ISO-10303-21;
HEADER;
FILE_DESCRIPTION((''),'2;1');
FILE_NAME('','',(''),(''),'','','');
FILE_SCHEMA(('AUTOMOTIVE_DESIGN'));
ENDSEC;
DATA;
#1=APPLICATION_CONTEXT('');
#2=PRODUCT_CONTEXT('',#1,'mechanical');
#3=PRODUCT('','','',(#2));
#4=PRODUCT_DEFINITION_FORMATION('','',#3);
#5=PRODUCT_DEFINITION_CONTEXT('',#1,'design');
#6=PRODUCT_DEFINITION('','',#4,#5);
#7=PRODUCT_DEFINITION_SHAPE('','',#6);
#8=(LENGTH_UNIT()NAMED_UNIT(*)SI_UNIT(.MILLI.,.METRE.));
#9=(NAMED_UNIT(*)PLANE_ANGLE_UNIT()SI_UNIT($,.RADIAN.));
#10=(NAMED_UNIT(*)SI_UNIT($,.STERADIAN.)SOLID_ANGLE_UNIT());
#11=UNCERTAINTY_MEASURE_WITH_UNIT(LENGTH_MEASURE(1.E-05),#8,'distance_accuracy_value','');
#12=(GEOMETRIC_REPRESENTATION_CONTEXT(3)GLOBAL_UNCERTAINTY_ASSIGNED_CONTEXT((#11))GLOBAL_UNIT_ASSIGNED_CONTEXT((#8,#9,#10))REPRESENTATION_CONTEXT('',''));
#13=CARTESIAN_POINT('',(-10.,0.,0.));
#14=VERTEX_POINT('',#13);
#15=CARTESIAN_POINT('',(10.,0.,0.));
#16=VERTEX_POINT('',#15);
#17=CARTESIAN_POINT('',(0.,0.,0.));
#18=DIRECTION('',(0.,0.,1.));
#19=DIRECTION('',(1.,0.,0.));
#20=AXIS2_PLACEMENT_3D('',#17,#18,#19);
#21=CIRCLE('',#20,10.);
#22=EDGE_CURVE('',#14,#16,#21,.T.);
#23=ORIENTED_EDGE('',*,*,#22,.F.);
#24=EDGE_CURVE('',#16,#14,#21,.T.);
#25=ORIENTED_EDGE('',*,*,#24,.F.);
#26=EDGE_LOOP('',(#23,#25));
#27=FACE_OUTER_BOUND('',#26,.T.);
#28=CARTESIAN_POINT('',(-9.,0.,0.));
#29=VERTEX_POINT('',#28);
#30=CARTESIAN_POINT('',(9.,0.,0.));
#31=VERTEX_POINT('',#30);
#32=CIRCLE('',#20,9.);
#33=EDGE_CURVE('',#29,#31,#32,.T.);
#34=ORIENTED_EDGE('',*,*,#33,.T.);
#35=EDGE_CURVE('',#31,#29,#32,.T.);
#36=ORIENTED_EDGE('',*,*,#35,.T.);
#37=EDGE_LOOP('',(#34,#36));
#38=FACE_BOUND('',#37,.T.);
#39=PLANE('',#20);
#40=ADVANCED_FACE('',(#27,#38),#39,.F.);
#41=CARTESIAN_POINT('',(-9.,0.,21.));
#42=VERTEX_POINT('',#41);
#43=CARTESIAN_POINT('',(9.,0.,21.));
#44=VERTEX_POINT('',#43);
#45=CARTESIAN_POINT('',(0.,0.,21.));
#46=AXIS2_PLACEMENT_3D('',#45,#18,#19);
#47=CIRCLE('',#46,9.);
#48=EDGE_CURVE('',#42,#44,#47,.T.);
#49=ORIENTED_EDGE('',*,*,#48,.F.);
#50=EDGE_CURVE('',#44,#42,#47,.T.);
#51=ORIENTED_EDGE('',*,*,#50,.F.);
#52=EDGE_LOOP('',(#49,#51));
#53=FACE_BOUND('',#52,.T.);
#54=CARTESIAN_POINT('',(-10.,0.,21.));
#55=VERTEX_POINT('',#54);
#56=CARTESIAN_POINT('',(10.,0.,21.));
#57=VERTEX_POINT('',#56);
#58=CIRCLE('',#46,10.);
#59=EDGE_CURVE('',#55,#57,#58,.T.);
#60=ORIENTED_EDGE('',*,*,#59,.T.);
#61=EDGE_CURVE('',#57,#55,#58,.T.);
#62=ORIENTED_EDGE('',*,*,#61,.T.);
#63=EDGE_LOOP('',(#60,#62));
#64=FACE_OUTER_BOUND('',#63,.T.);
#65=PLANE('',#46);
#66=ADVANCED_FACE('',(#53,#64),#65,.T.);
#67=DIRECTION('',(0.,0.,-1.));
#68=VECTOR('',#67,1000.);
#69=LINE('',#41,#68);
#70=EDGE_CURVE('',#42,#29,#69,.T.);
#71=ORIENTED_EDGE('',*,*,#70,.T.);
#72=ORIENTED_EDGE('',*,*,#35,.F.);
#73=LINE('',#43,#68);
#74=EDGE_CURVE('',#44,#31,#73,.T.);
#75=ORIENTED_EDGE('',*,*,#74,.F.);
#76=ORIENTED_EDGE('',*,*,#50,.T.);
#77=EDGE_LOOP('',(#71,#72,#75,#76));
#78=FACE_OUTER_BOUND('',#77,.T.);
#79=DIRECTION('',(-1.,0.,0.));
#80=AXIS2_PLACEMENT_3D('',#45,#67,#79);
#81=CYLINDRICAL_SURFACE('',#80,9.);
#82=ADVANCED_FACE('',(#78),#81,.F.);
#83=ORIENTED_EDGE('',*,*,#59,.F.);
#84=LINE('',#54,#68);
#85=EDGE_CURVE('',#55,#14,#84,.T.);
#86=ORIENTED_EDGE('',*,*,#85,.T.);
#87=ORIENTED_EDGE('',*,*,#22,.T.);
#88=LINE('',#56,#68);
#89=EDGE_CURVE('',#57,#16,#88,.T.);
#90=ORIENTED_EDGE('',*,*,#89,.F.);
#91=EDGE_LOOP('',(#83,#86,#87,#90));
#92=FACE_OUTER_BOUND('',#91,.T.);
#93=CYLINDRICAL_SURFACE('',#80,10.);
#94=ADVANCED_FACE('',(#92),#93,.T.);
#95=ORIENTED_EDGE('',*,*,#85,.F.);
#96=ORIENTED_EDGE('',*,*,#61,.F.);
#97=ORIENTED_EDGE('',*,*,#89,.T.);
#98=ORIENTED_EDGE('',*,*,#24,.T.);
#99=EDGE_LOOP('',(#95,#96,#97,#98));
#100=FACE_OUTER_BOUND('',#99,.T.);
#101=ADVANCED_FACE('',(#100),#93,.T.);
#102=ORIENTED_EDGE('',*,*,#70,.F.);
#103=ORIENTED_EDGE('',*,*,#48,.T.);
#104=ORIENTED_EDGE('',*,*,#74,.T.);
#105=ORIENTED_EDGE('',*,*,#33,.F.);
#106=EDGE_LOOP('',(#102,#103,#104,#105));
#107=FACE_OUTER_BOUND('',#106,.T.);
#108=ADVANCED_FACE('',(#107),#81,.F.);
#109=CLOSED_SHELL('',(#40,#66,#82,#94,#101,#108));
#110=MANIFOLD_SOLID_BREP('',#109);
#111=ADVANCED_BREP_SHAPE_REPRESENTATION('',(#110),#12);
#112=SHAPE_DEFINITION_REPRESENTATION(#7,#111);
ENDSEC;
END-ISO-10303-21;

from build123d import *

# Parameters (mm, degrees)
SKETCH_1_R      = 10
SKETCH_1_R_2    = 9
EXTRUDE_1_DEPTH = 21


with BuildPart() as part:
    # 草图1 → 凸台-拉伸1 (new body)
    with BuildSketch(Plane.XY):
        with Locations(Location((0, 0, 0), (0, 0, 180))):
            Circle(SKETCH_1_R)
        with Locations(Location((0, 0, 0), (0, 0, 180))):
            Circle(SKETCH_1_R_2, mode=Mode.SUBTRACT)
    extrude(amount=EXTRUDE_1_DEPTH)


solid = part.part
